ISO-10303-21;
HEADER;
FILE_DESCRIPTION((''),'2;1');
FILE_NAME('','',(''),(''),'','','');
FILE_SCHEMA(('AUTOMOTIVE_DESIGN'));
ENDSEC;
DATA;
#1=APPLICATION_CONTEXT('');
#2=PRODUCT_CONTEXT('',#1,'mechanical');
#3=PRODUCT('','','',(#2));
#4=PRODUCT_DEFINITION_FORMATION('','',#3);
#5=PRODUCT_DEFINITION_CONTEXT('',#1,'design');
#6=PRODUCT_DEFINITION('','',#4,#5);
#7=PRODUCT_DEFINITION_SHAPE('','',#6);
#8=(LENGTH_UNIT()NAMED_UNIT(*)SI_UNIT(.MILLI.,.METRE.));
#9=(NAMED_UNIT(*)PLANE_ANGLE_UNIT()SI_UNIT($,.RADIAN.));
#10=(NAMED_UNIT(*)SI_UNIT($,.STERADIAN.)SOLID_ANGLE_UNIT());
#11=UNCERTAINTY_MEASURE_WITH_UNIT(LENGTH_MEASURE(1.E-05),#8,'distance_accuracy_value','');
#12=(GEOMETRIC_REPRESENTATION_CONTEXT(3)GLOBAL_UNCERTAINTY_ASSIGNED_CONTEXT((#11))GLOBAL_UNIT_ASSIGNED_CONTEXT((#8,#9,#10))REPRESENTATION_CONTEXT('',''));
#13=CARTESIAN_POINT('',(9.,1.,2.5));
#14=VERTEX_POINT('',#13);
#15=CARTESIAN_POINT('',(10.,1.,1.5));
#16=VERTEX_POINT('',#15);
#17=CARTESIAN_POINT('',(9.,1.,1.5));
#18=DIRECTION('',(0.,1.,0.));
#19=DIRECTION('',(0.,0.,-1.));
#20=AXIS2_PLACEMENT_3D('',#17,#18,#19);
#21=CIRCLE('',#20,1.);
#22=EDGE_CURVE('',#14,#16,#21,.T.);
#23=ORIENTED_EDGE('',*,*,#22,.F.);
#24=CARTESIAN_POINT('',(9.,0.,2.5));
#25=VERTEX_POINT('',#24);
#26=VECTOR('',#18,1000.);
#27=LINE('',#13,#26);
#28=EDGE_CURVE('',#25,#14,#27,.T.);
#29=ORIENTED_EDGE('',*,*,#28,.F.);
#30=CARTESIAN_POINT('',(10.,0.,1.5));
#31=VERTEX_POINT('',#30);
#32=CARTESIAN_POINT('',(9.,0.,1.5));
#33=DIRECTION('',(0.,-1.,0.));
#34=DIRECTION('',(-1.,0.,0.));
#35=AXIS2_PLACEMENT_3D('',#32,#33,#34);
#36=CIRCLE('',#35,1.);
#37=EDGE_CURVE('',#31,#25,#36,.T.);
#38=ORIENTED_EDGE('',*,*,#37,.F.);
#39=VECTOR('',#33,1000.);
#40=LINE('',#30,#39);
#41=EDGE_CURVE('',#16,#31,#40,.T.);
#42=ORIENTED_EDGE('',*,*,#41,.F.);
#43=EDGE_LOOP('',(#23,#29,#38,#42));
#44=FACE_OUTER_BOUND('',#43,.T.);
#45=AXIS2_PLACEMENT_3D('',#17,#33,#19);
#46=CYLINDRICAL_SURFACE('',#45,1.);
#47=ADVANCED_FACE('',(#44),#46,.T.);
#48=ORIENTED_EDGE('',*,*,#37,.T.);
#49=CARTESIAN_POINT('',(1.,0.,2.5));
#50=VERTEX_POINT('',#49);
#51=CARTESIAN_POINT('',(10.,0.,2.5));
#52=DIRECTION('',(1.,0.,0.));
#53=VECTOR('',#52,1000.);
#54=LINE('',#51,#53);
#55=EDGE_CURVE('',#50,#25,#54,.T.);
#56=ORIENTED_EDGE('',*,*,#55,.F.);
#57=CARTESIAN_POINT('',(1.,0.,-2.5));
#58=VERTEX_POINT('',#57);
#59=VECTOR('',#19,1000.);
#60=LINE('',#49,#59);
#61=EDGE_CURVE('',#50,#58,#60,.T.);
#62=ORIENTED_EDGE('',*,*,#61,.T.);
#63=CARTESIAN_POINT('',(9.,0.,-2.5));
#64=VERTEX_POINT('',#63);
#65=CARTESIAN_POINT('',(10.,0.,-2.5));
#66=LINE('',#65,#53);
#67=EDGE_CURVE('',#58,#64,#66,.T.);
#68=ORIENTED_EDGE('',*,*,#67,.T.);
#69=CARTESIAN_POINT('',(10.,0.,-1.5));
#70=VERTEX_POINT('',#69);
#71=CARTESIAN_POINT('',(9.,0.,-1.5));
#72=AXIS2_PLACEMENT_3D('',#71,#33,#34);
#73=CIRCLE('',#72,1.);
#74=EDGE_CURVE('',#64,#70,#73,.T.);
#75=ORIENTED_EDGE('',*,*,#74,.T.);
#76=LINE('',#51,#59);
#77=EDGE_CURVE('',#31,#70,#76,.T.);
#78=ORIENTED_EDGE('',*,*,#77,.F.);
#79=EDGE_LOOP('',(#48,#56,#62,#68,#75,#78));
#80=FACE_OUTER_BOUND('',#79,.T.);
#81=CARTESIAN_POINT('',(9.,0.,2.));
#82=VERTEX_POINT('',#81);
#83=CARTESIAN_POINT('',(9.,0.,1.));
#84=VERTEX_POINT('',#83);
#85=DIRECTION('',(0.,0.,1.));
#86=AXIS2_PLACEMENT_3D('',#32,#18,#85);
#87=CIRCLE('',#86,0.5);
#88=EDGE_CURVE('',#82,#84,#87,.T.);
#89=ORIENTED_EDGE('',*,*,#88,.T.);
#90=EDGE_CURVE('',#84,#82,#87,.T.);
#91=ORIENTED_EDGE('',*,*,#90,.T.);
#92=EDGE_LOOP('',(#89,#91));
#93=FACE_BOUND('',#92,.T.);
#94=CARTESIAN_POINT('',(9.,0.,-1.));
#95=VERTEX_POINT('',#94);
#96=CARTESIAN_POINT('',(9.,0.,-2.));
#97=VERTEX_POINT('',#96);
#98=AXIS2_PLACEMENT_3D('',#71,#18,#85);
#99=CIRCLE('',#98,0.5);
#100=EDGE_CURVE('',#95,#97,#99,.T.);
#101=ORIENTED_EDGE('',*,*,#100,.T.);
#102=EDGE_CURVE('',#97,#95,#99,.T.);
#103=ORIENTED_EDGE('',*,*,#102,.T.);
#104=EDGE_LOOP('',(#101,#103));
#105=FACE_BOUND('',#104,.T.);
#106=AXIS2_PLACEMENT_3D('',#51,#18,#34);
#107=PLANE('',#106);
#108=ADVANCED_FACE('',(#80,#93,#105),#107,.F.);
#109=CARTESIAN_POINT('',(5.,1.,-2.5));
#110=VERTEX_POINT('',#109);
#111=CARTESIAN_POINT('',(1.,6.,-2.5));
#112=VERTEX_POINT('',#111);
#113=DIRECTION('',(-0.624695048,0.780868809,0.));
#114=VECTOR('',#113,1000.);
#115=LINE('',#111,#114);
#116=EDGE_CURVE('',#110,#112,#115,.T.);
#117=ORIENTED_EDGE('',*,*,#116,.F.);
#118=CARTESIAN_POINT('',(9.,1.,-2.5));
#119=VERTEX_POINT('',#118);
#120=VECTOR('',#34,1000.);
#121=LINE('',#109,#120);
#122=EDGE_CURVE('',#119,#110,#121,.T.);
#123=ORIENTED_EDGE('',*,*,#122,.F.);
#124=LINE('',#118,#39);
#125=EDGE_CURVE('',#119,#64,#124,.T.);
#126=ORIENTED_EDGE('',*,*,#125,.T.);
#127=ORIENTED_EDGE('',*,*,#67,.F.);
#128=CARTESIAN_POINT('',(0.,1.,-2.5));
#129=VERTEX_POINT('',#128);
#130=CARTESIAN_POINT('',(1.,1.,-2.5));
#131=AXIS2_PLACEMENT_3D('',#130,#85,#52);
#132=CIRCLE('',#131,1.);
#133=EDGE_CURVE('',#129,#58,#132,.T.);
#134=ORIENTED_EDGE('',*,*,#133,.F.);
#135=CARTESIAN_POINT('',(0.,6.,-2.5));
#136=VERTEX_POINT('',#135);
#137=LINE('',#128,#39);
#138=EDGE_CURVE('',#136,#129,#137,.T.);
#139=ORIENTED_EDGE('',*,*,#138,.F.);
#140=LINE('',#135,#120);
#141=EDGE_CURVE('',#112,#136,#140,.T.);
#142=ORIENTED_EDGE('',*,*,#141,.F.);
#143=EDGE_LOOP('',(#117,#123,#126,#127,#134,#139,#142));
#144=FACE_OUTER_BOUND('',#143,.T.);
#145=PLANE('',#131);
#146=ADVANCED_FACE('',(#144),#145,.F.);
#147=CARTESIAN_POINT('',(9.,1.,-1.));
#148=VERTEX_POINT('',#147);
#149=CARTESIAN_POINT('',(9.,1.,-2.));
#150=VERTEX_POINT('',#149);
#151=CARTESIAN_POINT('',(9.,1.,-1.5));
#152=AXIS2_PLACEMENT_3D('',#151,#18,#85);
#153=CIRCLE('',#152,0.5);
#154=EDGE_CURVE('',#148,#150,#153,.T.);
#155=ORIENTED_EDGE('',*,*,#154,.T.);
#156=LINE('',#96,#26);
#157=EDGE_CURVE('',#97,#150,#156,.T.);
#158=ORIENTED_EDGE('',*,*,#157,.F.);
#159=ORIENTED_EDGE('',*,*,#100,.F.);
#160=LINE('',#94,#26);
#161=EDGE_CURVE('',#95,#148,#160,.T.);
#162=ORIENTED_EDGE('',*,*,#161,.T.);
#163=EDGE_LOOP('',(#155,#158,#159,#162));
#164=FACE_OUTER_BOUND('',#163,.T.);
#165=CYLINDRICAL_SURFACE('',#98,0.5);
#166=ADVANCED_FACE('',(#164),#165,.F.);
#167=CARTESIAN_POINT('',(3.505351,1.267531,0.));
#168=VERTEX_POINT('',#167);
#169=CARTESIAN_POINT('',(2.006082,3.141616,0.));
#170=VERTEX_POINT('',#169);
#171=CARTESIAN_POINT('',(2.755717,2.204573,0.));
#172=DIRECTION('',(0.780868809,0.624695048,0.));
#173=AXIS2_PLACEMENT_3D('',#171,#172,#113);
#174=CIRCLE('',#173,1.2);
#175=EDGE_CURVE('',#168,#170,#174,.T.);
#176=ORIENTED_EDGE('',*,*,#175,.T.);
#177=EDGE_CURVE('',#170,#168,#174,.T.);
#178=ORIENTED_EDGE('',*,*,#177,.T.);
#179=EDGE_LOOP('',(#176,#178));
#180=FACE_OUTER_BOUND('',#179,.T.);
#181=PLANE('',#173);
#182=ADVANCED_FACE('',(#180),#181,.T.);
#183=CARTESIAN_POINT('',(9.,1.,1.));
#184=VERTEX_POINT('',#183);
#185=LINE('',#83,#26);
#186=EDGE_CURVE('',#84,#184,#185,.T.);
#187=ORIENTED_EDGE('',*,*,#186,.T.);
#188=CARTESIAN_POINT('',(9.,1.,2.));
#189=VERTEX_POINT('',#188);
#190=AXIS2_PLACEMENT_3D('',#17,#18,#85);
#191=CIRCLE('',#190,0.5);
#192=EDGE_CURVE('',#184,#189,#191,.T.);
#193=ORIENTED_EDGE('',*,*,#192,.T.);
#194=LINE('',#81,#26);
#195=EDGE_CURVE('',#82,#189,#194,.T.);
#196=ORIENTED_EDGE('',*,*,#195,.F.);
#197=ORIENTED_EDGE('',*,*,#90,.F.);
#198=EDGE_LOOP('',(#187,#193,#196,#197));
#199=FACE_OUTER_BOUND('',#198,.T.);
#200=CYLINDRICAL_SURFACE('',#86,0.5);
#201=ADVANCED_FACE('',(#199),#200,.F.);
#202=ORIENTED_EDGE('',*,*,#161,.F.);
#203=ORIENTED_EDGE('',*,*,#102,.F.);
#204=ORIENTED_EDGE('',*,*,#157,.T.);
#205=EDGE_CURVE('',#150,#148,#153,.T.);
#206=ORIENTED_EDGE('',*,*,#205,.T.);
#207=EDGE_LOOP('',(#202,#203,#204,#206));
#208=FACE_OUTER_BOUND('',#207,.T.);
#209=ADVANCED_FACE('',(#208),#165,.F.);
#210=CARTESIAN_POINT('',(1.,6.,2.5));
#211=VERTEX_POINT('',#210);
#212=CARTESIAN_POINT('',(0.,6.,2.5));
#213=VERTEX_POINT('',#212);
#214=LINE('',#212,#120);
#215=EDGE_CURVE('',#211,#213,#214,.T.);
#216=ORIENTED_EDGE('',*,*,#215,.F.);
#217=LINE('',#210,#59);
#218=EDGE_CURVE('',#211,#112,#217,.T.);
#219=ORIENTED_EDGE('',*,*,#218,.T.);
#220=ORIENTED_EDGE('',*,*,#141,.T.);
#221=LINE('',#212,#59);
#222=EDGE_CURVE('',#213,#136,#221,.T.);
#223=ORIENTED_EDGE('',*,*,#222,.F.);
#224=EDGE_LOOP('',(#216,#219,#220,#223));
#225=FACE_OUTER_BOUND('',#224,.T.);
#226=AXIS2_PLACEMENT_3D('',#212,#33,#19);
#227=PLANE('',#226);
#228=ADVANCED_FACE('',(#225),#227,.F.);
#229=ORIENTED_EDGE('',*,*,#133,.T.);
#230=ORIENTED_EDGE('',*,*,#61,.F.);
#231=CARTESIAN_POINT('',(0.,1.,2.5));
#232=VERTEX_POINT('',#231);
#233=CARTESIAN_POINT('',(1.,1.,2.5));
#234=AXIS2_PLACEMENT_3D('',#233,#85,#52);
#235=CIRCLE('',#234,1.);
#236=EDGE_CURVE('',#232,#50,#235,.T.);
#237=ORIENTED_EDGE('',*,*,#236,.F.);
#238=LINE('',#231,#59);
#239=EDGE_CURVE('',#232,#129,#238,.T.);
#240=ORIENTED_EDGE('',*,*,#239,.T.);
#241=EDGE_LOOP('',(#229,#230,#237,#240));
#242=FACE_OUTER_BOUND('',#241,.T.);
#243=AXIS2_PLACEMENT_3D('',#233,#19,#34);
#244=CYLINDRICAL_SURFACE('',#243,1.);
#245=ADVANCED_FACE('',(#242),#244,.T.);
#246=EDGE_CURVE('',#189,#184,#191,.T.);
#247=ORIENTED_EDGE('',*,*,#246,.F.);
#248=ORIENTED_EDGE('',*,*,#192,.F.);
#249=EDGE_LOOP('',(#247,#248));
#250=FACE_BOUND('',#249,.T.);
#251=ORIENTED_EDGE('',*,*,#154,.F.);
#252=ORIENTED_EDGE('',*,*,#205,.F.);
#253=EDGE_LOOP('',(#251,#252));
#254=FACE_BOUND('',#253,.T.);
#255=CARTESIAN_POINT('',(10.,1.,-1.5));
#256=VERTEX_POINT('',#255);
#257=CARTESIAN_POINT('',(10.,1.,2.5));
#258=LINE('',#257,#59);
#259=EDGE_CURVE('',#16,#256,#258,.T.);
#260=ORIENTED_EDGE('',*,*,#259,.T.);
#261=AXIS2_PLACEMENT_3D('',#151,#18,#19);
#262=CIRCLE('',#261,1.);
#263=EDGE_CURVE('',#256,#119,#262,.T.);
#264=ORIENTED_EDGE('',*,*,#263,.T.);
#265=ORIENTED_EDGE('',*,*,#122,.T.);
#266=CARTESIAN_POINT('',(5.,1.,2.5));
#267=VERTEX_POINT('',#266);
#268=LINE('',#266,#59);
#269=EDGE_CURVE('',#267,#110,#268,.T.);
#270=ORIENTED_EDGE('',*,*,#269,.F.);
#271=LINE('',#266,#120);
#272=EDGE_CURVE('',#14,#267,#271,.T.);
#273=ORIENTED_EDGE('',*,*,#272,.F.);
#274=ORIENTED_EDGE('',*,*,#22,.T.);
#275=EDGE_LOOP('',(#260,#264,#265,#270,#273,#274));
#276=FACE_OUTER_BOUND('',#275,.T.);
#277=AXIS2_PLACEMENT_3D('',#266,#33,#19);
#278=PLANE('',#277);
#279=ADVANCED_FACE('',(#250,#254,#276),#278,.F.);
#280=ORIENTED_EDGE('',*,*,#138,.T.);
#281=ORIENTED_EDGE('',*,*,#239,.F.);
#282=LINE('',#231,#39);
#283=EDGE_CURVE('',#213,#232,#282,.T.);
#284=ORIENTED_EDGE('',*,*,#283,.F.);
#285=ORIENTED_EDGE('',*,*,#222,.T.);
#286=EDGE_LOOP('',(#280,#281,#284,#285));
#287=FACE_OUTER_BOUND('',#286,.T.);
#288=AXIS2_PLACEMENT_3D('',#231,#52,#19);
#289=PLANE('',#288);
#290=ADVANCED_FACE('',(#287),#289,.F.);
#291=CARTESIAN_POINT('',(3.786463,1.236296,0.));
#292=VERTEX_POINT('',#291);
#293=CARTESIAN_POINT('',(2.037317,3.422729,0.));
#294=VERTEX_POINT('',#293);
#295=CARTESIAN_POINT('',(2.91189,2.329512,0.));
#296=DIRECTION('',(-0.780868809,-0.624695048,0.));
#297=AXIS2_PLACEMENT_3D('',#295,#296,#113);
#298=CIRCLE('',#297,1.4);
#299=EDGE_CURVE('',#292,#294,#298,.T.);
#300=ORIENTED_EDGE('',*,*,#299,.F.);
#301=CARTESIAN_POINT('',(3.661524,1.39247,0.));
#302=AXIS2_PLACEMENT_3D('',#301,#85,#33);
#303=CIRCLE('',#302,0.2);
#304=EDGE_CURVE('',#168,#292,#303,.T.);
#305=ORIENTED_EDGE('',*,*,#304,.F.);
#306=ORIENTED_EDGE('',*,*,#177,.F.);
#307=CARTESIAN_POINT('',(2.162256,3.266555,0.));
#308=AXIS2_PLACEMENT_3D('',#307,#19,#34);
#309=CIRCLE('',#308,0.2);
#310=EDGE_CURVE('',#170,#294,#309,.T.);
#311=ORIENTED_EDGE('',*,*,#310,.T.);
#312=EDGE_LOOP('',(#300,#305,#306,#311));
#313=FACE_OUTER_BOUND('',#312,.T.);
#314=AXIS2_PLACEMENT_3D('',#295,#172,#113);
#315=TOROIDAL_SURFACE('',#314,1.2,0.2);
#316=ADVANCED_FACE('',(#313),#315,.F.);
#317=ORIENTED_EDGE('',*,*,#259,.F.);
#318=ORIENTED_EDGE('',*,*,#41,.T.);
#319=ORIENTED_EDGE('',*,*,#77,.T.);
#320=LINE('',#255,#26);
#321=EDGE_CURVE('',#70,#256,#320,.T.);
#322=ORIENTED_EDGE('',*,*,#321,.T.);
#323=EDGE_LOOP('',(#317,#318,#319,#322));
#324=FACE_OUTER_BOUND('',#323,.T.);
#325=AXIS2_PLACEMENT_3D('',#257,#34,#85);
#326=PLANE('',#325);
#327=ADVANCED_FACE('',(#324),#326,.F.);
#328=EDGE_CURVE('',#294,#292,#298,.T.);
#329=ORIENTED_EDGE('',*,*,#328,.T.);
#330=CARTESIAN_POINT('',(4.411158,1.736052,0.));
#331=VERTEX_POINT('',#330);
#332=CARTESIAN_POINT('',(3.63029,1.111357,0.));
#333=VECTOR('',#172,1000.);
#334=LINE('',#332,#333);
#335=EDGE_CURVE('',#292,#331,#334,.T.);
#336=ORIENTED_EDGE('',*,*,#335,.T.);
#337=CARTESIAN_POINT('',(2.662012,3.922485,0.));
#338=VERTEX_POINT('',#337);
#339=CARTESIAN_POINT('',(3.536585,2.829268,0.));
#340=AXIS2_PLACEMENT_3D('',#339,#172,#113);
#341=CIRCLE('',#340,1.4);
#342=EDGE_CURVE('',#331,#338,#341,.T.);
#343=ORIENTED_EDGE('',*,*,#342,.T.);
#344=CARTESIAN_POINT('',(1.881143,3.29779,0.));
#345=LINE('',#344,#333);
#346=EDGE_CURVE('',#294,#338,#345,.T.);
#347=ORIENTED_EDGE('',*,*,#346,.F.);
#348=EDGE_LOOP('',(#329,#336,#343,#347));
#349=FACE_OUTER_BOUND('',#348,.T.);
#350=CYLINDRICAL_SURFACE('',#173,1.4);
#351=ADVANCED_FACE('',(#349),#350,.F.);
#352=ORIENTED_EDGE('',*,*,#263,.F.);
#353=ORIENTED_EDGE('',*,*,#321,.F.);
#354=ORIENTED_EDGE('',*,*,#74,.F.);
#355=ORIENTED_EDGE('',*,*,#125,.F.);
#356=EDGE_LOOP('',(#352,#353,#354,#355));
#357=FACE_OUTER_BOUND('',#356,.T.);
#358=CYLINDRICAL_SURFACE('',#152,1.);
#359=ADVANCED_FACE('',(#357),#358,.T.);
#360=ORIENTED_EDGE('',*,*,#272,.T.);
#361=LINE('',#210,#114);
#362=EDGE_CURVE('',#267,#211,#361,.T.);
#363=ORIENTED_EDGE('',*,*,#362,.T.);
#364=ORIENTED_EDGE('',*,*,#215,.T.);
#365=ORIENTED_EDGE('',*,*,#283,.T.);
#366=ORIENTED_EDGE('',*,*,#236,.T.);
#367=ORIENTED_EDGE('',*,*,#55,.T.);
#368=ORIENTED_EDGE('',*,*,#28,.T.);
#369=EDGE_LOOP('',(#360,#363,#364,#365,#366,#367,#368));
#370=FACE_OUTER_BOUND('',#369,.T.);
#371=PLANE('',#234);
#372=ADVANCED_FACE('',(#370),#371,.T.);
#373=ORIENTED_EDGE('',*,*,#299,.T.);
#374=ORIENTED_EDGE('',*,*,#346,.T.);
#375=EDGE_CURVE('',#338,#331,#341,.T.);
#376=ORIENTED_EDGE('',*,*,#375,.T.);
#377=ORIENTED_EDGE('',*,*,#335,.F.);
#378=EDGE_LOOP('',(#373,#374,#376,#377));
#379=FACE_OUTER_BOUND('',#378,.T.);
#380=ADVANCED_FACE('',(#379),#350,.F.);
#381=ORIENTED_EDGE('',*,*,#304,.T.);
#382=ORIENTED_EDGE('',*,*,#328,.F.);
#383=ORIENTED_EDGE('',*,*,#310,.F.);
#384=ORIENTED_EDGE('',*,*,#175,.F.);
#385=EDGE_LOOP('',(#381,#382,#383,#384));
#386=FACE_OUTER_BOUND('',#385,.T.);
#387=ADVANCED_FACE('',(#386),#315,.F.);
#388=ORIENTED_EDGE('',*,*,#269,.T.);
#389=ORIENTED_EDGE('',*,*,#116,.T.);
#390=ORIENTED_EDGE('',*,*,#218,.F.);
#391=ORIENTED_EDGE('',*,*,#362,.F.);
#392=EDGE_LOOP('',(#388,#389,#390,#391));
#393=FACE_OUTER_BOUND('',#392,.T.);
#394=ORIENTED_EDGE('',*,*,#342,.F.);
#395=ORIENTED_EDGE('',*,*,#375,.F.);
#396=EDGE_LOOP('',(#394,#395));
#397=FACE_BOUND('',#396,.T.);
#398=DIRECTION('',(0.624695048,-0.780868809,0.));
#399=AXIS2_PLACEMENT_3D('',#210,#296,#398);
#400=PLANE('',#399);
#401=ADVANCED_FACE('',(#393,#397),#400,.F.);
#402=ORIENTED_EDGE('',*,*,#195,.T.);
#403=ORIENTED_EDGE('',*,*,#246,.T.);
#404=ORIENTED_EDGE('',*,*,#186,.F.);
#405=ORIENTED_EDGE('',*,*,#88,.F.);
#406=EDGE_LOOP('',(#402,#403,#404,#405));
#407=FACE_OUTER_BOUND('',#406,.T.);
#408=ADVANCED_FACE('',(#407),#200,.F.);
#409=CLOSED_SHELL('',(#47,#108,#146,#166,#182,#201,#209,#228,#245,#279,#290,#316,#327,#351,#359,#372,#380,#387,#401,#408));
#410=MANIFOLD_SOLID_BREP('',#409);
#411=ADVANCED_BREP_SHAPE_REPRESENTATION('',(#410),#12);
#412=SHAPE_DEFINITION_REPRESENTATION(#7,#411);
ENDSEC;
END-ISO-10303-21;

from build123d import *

# Parameters (mm, degrees)
BRACKET_BODY_DEPTH        = 2.5
FACE_RECESS_SKETCH_R      = 1.4
FACE_RECESS_2_8X1_DEPTH   = 1
MOUNTING_HOLES_SKETCH_R   = 0.5
FOOT_MOUNTING_HOLES_DEPTH = 12.456439237
CORNER_FILLETS_R1_R       = 1
RECESS_EDGE_FILLET_R0_2_R = 0.2


with BuildPart() as part:
    # Bracket Profile Sketch → Bracket Body (new, symmetric)
    with BuildSketch(Plane.XY):
        with BuildLine():
            Line((0, 1), (0, 6))
            Line((0, 6), (1, 6))
            Line((1, 6), (5, 1))
            Line((5, 1), (10, 1))
            Line((10, 1), (10, 0))
            Line((10, 0), (1, 0))
            ThreePointArc((1, 0), (0.292893219, 0.292893219), (0, 1))
        make_face()
    extrude(amount=BRACKET_BODY_DEPTH, both=True)

    # Face Recess Sketch → Face Recess Ø2.8x1 (cut)
    with BuildSketch(Plane(origin=(3.536585366, 2.829268293, 0), x_dir=(0, 0, -1), z_dir=(0.7808688094430304, 0.6246950475544242, 0))):
        with Locations(Location((0, 0, 0), (0, 0, 90))):
            Circle(FACE_RECESS_SKETCH_R)
    extrude(amount=-FACE_RECESS_2_8X1_DEPTH, mode=Mode.SUBTRACT)

    # Mounting Holes Sketch → Foot Mounting Holes (cut, through all)
    with BuildSketch(Plane(origin=(0, 1, 0), x_dir=(1, 0, 0), z_dir=(0, 1, 0))):
        with Locations(Location((9, -1.5, 0), (0, 0, 270))):
            Circle(MOUNTING_HOLES_SKETCH_R)
        with Locations(Location((9, 1.5, 0), (0, 0, 270))):
            Circle(MOUNTING_HOLES_SKETCH_R)
    extrude(amount=-FOOT_MOUNTING_HOLES_DEPTH, mode=Mode.SUBTRACT)

    # Corner Fillets R1
    corner_fillets_r1_edges = [part.edges().sort_by_distance(p)[0] for p in [
        (10, 0.5, 2.5),
        (10, 0.5, -2.5),
    ]]
    fillet(corner_fillets_r1_edges, radius=CORNER_FILLETS_R1_R)

    # Recess Edge Fillet R0.2
    recess_edge_fillet_r0_2_edges = [part.edges().sort_by_distance(p)[0] for p in [
        (3.630289623, 1.111356912, 0),
    ]]
    fillet(recess_edge_fillet_r0_2_edges, radius=RECESS_EDGE_FILLET_R0_2_R)


solid = part.part
